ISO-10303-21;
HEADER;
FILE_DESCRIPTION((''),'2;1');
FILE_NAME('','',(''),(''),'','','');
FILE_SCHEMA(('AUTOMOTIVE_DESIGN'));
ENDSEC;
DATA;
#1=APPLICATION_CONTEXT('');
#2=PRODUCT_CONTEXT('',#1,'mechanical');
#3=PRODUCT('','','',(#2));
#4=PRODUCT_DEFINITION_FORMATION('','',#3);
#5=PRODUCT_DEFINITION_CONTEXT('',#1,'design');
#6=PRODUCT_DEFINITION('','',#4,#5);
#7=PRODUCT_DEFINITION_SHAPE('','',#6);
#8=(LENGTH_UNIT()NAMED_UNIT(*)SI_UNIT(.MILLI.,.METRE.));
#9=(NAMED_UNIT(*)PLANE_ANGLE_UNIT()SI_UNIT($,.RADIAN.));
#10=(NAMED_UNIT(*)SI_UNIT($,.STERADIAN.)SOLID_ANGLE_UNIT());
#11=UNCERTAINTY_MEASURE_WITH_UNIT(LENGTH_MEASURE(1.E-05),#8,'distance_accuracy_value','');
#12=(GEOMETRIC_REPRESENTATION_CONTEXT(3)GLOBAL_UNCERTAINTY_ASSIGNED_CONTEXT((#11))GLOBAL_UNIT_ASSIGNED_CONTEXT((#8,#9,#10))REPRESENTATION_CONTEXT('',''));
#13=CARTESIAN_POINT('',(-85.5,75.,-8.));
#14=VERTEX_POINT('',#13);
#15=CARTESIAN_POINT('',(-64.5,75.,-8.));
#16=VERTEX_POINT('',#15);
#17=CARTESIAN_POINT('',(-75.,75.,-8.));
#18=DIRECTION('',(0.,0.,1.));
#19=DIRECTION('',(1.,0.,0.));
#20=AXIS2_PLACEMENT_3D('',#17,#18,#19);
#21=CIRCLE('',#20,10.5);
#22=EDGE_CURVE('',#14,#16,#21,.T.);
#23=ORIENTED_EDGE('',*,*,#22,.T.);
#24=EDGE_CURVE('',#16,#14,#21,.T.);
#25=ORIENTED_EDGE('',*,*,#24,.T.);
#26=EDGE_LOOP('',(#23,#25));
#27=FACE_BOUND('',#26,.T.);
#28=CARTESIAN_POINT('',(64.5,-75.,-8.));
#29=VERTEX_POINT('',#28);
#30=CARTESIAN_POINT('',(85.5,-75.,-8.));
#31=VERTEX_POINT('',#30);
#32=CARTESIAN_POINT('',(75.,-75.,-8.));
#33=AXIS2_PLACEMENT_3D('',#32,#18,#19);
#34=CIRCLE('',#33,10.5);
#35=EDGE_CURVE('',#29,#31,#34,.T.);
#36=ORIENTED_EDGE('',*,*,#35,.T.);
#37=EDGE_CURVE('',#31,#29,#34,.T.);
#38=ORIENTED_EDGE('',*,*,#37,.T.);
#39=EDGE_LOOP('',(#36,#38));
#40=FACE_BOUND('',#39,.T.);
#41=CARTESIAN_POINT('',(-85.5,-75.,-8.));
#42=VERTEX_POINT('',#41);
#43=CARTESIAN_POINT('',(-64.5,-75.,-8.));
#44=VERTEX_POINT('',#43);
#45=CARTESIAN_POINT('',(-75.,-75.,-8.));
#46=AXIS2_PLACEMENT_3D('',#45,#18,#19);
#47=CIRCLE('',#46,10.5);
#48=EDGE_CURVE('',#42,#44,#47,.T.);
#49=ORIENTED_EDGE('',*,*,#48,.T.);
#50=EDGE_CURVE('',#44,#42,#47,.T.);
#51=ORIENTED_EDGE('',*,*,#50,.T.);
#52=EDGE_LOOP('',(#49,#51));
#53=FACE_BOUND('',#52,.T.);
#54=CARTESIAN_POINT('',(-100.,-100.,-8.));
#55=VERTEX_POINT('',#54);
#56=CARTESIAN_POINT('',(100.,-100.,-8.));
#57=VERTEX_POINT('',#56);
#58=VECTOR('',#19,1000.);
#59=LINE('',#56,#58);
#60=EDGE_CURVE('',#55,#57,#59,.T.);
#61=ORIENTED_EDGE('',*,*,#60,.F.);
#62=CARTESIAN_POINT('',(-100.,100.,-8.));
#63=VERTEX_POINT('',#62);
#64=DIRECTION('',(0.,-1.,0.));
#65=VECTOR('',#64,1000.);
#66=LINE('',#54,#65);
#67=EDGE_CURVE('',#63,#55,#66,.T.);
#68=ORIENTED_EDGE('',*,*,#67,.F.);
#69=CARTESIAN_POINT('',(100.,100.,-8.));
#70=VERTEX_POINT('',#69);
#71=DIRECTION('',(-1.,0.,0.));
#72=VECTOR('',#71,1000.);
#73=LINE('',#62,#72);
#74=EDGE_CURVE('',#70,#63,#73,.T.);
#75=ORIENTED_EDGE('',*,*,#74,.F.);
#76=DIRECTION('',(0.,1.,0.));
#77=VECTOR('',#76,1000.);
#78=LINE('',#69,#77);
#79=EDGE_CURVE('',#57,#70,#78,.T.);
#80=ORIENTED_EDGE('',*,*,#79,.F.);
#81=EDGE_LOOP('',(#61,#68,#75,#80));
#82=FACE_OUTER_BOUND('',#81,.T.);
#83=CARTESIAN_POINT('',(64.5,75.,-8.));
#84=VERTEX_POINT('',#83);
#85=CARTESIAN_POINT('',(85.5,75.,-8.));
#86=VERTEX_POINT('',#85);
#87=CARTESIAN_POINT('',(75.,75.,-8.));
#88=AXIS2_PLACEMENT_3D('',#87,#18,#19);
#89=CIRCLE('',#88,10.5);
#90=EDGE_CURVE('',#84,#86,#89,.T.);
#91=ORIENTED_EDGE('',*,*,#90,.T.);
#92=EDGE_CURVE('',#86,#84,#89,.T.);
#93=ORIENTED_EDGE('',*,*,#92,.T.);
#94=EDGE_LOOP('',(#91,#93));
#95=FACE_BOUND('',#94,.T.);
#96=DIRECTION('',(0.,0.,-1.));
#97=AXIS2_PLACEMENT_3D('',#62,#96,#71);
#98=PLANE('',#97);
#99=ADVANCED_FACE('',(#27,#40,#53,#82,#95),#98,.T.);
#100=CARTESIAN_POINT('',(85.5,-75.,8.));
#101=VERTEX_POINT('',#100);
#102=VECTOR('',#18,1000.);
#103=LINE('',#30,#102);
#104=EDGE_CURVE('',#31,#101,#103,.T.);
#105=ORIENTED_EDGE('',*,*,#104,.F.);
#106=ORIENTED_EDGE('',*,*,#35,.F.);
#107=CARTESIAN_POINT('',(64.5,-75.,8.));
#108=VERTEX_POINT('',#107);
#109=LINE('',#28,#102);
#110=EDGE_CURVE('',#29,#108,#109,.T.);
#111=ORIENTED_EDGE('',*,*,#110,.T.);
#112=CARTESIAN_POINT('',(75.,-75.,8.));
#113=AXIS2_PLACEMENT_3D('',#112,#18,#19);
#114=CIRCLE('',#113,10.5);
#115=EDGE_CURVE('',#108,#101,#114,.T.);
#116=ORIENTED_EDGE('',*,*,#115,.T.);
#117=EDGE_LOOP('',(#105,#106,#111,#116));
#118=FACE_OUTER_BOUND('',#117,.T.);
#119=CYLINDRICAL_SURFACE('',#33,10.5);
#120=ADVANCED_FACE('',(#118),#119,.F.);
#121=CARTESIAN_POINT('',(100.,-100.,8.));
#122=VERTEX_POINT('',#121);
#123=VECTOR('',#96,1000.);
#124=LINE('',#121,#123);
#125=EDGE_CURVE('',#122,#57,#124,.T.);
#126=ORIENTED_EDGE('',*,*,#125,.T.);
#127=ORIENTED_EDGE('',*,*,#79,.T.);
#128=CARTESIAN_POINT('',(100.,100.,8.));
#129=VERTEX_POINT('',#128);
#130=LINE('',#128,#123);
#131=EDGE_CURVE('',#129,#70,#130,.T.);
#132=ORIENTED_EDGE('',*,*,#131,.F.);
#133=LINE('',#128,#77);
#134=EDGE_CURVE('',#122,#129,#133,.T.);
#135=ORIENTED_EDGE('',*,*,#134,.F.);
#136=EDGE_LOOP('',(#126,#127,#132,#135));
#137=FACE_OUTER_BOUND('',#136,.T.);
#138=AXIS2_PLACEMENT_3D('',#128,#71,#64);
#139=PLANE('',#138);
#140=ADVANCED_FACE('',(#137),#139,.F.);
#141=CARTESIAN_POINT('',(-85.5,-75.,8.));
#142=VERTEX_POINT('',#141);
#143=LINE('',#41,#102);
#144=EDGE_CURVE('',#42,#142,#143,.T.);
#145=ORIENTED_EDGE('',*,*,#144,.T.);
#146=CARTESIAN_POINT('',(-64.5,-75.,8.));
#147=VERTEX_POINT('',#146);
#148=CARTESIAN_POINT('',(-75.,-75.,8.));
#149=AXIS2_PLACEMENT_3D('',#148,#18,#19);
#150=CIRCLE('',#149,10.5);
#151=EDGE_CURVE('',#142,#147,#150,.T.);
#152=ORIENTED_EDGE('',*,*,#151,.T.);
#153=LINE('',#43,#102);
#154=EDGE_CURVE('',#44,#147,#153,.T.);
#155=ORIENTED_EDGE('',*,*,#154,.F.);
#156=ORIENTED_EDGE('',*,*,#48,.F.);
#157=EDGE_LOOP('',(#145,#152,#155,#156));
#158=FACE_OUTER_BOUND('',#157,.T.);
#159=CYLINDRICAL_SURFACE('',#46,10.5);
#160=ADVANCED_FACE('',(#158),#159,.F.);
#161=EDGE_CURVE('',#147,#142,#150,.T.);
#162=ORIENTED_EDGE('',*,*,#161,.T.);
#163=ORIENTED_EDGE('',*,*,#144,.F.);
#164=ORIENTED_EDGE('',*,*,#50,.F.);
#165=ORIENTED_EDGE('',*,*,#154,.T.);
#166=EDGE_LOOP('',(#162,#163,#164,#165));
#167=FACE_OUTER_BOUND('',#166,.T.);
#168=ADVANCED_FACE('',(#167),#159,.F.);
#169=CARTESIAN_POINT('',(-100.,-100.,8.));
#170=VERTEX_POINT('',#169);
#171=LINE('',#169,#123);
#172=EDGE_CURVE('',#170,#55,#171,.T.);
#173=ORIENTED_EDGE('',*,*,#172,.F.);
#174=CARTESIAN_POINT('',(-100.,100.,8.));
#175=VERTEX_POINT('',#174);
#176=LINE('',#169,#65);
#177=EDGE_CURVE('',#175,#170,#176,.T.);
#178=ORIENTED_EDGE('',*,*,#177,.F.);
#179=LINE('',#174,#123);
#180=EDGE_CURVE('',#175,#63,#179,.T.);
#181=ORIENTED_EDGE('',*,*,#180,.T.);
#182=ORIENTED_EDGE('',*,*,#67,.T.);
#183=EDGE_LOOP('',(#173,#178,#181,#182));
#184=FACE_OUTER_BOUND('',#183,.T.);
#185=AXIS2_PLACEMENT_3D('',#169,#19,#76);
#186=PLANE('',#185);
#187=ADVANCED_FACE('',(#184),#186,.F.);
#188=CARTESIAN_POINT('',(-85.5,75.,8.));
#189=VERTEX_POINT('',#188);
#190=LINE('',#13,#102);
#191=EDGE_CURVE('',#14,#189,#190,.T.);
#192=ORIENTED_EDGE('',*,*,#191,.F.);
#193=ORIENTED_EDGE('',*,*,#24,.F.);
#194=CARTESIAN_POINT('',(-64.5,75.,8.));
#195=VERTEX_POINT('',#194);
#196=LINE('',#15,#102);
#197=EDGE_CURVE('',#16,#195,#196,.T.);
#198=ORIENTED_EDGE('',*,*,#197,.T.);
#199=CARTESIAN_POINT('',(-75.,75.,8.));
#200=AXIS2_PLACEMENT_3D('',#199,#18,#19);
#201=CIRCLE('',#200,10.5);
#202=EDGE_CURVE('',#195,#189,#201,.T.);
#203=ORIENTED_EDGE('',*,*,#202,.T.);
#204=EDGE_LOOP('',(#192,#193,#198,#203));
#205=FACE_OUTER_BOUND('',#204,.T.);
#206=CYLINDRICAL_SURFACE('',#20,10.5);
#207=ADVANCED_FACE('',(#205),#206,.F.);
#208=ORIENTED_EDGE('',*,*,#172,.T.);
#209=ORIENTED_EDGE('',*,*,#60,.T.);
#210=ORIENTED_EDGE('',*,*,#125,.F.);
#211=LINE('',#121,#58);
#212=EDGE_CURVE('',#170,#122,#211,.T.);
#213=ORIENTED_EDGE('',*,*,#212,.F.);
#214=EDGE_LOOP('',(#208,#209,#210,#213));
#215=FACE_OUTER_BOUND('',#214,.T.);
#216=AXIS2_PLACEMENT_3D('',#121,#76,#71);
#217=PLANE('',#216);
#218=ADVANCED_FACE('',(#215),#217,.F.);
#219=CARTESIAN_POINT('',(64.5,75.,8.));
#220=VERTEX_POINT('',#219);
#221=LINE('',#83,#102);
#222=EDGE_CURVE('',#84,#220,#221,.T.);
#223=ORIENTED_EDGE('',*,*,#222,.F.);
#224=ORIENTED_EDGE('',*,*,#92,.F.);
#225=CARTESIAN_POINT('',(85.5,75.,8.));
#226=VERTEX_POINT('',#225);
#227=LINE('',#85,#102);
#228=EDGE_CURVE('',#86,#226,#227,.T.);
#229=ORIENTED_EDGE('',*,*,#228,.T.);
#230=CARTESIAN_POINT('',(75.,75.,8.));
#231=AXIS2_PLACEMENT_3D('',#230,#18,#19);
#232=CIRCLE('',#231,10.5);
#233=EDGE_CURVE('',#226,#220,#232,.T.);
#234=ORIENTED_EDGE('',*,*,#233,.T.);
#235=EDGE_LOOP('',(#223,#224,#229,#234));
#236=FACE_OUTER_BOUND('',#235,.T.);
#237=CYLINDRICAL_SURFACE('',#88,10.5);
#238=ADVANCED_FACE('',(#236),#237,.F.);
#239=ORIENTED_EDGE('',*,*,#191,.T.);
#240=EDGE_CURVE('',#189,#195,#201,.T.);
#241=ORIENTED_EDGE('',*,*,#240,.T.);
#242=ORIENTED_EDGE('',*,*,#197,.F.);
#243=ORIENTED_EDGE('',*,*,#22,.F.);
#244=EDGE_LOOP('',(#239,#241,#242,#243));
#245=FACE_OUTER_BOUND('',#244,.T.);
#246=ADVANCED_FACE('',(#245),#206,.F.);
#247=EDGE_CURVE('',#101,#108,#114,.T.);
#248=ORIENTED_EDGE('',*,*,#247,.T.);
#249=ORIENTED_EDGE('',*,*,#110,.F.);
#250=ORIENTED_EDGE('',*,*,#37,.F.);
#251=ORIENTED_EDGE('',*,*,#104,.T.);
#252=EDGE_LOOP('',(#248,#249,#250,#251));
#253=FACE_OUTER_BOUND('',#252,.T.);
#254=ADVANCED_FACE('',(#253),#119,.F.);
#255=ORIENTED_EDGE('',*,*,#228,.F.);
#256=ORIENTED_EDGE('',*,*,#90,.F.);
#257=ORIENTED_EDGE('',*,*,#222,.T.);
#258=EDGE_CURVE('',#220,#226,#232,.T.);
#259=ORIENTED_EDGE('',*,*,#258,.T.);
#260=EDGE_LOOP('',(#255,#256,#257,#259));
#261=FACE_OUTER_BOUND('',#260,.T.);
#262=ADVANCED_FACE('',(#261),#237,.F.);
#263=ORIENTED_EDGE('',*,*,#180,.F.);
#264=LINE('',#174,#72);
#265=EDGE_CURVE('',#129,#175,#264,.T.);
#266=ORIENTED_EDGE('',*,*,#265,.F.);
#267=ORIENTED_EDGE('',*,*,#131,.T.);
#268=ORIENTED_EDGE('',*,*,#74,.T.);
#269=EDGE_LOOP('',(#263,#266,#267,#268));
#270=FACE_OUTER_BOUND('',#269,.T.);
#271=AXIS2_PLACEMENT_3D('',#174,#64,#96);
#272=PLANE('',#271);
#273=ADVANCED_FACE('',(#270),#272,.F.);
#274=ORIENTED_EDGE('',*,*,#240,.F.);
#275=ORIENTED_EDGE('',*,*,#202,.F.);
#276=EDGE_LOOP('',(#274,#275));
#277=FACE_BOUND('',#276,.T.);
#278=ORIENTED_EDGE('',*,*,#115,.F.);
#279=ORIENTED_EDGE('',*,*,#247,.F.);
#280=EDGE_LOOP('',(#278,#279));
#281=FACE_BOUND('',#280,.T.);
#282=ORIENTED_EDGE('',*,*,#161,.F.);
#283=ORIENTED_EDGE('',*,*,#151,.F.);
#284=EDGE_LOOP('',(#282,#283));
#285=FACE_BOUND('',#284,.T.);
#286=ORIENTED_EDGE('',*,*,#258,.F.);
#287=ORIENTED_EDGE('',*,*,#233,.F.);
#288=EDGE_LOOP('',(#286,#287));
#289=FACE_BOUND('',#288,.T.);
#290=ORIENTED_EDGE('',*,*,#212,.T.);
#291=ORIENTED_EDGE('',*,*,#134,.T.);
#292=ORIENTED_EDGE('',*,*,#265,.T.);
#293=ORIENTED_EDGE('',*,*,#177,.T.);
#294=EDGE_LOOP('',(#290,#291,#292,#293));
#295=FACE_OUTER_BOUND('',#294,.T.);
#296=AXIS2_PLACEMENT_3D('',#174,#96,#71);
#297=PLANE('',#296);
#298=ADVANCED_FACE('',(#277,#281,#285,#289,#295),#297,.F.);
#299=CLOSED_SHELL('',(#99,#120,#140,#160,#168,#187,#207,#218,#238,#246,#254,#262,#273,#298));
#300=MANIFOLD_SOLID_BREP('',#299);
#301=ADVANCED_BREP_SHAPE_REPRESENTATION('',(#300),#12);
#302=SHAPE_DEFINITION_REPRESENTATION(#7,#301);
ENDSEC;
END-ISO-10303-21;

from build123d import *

# Parameters (mm, degrees)
SKETCH1_W      = 200
SKETCH1_H      = 200
EXTRUDE1_DEPTH = 8
SKETCH2_R      = 10.5
EXTRUDE2_DEPTH = 143.323574997


with BuildPart() as part:
    # Sketch1 → Extrude1 (new, symmetric)
    with BuildSketch(Plane.XY):
        Rectangle(SKETCH1_W, SKETCH1_H)
    extrude(amount=EXTRUDE1_DEPTH, both=True)

    # Sketch2 → Extrude2 (cut, through all)
    with BuildSketch(Plane.XY.offset(8)):
        with Locations((-75, 75)):
            Circle(SKETCH2_R)
        with Locations((75, 75)):
            Circle(SKETCH2_R)
        with Locations((-75, -75)):
            Circle(SKETCH2_R)
        with Locations((75, -75)):
            Circle(SKETCH2_R)
    extrude(amount=-EXTRUDE2_DEPTH, mode=Mode.SUBTRACT)


solid = part.part
